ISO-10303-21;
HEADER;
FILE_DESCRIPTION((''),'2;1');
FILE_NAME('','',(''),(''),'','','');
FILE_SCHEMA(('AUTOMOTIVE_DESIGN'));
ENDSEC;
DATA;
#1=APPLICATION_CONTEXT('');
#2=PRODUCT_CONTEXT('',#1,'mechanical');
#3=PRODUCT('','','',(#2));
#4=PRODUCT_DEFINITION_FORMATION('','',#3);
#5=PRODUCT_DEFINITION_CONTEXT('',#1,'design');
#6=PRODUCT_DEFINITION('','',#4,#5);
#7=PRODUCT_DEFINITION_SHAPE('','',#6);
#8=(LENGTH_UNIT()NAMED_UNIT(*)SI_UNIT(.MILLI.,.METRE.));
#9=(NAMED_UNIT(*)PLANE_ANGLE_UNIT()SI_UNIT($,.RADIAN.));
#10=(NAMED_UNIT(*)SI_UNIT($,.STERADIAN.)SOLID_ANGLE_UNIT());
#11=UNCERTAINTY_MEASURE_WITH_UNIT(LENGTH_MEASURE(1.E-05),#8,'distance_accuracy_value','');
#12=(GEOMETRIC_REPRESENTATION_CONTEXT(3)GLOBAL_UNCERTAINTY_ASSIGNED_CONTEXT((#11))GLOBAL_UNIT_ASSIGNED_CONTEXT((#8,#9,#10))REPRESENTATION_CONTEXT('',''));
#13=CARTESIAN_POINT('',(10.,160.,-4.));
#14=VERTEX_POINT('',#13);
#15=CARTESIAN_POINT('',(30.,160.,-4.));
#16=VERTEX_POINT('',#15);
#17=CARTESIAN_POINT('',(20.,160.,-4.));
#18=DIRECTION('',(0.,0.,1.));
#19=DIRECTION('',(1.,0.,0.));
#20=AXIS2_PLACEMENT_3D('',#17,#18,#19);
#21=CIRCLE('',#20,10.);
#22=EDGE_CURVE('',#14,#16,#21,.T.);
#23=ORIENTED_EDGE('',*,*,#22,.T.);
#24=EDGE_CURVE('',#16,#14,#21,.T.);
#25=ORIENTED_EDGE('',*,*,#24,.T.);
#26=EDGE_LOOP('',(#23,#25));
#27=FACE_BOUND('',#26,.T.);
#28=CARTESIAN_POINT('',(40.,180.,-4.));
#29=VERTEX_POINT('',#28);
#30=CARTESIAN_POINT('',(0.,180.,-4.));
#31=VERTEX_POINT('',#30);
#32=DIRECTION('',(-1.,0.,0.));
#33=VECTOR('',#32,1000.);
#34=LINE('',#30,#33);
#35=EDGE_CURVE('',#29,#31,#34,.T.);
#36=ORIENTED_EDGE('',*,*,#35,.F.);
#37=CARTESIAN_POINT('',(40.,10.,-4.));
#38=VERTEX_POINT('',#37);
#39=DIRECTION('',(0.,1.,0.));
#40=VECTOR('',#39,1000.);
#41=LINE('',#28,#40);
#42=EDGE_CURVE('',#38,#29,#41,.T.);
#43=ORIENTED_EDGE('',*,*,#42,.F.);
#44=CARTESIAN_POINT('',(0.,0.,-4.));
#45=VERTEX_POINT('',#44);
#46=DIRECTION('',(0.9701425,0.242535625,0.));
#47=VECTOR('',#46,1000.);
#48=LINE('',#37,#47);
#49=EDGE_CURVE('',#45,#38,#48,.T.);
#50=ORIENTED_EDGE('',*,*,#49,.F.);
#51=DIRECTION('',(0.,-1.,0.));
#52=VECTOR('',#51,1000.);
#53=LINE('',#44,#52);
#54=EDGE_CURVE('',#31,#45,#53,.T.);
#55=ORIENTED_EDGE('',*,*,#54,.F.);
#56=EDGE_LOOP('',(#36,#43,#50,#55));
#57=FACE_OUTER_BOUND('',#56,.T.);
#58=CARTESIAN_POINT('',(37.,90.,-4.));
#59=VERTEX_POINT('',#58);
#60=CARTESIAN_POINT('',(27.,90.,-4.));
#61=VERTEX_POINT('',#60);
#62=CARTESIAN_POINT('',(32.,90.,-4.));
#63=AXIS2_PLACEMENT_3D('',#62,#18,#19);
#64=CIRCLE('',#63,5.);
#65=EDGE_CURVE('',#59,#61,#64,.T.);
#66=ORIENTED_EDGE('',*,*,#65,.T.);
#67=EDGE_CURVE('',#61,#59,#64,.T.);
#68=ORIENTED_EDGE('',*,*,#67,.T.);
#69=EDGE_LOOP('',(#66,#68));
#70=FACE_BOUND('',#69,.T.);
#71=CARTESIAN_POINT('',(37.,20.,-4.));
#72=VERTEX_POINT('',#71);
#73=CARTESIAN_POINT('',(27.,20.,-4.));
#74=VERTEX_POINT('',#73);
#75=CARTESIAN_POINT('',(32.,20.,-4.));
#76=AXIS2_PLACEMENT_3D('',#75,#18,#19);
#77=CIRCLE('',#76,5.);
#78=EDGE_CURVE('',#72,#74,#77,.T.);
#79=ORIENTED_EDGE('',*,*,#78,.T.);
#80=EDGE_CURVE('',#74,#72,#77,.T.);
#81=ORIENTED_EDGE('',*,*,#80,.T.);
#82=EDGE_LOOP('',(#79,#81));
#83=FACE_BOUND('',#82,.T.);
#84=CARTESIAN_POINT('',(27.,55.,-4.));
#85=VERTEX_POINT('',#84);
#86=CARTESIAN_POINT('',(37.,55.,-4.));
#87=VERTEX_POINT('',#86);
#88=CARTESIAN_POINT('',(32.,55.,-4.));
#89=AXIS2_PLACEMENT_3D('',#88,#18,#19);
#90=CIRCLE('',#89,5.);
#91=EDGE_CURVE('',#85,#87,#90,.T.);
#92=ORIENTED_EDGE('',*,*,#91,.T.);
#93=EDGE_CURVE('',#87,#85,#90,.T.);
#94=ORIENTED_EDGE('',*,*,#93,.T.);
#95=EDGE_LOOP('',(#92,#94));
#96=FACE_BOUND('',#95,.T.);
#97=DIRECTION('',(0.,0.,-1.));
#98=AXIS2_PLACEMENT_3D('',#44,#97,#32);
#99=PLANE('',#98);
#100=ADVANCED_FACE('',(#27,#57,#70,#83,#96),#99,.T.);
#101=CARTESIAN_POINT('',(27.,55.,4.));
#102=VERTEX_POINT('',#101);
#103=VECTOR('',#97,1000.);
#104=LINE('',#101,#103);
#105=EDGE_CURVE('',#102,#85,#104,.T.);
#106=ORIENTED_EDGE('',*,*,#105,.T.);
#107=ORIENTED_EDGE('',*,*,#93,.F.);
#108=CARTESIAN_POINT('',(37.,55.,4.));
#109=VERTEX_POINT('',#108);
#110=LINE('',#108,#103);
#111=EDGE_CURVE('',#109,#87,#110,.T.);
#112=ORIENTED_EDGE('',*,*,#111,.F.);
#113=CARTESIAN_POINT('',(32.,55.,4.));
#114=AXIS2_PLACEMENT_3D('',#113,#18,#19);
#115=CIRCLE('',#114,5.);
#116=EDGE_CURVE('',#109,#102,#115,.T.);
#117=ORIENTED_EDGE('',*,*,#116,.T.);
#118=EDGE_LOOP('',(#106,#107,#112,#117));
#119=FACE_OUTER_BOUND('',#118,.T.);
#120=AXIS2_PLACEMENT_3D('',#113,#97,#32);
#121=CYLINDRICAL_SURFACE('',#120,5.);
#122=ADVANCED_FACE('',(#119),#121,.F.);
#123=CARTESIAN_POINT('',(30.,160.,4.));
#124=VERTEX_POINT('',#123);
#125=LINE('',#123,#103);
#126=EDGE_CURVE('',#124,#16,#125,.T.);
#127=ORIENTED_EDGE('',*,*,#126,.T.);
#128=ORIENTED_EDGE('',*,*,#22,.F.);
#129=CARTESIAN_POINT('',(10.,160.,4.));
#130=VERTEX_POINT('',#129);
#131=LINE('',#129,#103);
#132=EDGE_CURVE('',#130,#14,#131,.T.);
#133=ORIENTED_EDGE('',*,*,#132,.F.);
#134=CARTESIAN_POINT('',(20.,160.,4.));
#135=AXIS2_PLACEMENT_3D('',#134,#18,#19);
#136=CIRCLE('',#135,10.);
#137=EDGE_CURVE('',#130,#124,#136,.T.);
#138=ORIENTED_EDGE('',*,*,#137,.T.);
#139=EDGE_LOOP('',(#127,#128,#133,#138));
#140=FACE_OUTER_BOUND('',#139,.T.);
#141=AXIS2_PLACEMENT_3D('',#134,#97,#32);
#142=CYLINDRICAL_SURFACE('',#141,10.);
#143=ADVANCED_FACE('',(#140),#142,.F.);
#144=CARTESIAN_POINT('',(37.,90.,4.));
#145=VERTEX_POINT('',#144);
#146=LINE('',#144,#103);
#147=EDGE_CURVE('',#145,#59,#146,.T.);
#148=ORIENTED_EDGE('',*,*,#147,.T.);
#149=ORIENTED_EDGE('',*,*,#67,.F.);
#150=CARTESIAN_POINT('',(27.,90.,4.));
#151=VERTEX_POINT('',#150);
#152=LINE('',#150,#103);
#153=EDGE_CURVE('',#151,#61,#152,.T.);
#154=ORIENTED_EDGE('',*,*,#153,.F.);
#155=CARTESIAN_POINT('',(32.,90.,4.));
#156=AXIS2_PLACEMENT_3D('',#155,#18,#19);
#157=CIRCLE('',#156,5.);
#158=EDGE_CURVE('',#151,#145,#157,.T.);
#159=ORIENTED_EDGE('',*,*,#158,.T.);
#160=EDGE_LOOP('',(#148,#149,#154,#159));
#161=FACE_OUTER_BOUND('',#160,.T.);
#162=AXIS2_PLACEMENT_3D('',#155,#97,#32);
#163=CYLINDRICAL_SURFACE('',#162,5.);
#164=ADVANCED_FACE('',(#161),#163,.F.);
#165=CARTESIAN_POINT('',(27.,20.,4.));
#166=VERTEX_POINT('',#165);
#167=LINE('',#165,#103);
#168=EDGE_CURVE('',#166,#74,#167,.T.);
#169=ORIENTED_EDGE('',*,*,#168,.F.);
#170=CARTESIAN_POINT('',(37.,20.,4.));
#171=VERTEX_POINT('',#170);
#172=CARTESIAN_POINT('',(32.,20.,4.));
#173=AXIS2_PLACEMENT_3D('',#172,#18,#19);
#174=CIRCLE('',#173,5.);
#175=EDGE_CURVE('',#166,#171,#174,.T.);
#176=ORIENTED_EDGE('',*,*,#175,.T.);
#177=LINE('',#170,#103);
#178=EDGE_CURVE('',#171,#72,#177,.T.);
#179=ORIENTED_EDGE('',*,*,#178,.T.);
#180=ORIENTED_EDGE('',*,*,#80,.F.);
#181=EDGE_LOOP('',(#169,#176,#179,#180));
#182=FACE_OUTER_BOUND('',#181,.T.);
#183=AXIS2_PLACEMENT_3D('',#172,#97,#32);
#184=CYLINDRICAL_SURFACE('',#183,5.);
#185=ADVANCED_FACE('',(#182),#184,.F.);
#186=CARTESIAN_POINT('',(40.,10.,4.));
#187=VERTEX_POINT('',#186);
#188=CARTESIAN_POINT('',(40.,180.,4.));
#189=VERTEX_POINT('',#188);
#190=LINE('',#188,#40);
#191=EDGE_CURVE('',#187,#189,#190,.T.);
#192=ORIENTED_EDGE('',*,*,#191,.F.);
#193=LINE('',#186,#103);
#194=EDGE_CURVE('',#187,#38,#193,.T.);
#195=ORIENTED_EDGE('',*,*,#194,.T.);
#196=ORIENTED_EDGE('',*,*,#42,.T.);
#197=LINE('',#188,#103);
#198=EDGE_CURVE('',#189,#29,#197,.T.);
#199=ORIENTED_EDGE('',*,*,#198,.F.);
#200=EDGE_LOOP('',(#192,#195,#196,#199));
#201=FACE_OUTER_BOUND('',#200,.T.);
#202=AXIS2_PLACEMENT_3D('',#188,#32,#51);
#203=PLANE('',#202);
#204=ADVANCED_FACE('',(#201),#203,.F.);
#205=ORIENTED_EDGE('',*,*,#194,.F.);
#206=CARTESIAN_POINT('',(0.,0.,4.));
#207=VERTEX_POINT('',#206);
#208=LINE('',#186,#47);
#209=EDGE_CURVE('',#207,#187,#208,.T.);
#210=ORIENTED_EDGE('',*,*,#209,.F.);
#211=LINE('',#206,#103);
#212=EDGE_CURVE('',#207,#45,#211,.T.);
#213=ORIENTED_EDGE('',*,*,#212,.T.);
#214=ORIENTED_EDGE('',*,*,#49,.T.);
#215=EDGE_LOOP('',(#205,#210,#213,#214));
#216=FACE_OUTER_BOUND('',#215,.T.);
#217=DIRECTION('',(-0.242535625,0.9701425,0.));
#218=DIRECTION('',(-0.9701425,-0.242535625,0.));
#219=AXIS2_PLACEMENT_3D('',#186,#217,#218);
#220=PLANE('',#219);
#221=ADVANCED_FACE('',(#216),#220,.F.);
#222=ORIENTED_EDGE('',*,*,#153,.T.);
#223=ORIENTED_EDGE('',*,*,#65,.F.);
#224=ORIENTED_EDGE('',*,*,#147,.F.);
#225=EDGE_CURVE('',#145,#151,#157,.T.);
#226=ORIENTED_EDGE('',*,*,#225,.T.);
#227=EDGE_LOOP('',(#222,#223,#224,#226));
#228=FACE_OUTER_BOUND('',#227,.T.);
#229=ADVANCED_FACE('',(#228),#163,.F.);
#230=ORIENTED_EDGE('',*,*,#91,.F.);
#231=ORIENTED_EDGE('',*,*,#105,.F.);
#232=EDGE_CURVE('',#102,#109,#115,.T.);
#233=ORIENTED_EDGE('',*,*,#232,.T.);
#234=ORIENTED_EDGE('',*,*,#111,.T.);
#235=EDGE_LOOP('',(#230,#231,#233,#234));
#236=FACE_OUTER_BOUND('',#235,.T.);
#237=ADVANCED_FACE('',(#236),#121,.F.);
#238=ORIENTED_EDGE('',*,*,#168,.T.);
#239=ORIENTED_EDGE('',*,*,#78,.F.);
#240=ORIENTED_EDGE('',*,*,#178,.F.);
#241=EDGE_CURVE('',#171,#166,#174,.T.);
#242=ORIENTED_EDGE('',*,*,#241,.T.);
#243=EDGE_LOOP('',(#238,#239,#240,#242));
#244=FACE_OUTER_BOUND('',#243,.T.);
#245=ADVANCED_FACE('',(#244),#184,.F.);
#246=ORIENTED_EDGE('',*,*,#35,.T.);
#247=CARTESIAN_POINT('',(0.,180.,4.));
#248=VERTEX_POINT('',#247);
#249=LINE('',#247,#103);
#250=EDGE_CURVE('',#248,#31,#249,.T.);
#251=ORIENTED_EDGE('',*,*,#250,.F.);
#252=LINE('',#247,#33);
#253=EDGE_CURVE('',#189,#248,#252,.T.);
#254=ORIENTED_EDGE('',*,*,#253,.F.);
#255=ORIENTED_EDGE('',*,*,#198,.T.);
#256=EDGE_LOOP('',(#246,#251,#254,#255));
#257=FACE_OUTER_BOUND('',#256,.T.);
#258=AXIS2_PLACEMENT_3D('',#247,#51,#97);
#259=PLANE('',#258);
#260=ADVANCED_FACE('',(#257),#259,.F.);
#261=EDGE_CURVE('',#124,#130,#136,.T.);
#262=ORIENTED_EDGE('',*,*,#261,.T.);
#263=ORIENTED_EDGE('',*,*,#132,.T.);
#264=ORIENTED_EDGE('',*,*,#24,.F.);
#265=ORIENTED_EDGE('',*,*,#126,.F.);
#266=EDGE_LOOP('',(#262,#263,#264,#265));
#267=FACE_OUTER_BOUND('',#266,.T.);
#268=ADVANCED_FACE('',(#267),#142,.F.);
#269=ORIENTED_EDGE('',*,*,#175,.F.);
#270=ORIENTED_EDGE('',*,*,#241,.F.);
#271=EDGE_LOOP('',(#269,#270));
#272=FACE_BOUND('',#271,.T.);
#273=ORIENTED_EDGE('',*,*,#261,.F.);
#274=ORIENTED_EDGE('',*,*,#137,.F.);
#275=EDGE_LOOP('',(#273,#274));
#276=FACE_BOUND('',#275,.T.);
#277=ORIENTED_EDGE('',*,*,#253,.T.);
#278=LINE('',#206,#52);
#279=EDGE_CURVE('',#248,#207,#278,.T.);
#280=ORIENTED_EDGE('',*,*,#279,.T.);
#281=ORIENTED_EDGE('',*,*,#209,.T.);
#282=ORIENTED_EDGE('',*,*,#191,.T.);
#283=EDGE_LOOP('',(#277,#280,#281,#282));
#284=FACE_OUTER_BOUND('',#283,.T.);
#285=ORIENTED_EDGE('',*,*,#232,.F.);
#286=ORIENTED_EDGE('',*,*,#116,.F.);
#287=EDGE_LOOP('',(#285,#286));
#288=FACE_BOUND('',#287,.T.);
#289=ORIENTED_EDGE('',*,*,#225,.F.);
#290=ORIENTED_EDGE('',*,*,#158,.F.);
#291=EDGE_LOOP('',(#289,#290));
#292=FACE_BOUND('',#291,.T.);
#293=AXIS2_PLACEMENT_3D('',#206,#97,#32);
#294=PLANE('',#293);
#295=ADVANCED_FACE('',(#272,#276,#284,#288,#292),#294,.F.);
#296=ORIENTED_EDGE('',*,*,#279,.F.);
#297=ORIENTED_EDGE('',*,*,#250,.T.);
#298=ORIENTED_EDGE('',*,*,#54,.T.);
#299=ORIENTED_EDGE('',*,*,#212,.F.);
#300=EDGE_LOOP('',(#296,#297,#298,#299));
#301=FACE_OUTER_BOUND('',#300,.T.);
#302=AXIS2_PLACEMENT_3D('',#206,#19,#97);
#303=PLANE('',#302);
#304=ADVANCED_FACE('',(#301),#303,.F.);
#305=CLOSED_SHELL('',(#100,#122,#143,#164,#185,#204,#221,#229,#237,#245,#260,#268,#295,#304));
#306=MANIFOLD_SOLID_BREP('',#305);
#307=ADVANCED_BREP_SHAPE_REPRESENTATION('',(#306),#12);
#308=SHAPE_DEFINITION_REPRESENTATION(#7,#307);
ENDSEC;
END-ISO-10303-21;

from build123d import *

# Parameters (mm, degrees)
SKETCH1_R           = 10
SKETCH1_R_2         = 5
BOSS_EXTRUDE1_DEPTH = 4


with BuildPart() as part:
    # Sketch1 → Boss-Extrude1 (new, symmetric)
    with BuildSketch(Plane.XY):
        Polygon((0, 0), (0, 180), (40, 180), (40, 10), align=None)
        with Locations((20, 160)):
            Circle(SKETCH1_R, mode=Mode.SUBTRACT)
        with Locations((32, 90)):
            Circle(SKETCH1_R_2, mode=Mode.SUBTRACT)
        with Locations((32, 55)):
            Circle(SKETCH1_R_2, mode=Mode.SUBTRACT)
        with Locations((32, 20)):
            Circle(SKETCH1_R_2, mode=Mode.SUBTRACT)
    extrude(amount=BOSS_EXTRUDE1_DEPTH, both=True)


solid = part.part
